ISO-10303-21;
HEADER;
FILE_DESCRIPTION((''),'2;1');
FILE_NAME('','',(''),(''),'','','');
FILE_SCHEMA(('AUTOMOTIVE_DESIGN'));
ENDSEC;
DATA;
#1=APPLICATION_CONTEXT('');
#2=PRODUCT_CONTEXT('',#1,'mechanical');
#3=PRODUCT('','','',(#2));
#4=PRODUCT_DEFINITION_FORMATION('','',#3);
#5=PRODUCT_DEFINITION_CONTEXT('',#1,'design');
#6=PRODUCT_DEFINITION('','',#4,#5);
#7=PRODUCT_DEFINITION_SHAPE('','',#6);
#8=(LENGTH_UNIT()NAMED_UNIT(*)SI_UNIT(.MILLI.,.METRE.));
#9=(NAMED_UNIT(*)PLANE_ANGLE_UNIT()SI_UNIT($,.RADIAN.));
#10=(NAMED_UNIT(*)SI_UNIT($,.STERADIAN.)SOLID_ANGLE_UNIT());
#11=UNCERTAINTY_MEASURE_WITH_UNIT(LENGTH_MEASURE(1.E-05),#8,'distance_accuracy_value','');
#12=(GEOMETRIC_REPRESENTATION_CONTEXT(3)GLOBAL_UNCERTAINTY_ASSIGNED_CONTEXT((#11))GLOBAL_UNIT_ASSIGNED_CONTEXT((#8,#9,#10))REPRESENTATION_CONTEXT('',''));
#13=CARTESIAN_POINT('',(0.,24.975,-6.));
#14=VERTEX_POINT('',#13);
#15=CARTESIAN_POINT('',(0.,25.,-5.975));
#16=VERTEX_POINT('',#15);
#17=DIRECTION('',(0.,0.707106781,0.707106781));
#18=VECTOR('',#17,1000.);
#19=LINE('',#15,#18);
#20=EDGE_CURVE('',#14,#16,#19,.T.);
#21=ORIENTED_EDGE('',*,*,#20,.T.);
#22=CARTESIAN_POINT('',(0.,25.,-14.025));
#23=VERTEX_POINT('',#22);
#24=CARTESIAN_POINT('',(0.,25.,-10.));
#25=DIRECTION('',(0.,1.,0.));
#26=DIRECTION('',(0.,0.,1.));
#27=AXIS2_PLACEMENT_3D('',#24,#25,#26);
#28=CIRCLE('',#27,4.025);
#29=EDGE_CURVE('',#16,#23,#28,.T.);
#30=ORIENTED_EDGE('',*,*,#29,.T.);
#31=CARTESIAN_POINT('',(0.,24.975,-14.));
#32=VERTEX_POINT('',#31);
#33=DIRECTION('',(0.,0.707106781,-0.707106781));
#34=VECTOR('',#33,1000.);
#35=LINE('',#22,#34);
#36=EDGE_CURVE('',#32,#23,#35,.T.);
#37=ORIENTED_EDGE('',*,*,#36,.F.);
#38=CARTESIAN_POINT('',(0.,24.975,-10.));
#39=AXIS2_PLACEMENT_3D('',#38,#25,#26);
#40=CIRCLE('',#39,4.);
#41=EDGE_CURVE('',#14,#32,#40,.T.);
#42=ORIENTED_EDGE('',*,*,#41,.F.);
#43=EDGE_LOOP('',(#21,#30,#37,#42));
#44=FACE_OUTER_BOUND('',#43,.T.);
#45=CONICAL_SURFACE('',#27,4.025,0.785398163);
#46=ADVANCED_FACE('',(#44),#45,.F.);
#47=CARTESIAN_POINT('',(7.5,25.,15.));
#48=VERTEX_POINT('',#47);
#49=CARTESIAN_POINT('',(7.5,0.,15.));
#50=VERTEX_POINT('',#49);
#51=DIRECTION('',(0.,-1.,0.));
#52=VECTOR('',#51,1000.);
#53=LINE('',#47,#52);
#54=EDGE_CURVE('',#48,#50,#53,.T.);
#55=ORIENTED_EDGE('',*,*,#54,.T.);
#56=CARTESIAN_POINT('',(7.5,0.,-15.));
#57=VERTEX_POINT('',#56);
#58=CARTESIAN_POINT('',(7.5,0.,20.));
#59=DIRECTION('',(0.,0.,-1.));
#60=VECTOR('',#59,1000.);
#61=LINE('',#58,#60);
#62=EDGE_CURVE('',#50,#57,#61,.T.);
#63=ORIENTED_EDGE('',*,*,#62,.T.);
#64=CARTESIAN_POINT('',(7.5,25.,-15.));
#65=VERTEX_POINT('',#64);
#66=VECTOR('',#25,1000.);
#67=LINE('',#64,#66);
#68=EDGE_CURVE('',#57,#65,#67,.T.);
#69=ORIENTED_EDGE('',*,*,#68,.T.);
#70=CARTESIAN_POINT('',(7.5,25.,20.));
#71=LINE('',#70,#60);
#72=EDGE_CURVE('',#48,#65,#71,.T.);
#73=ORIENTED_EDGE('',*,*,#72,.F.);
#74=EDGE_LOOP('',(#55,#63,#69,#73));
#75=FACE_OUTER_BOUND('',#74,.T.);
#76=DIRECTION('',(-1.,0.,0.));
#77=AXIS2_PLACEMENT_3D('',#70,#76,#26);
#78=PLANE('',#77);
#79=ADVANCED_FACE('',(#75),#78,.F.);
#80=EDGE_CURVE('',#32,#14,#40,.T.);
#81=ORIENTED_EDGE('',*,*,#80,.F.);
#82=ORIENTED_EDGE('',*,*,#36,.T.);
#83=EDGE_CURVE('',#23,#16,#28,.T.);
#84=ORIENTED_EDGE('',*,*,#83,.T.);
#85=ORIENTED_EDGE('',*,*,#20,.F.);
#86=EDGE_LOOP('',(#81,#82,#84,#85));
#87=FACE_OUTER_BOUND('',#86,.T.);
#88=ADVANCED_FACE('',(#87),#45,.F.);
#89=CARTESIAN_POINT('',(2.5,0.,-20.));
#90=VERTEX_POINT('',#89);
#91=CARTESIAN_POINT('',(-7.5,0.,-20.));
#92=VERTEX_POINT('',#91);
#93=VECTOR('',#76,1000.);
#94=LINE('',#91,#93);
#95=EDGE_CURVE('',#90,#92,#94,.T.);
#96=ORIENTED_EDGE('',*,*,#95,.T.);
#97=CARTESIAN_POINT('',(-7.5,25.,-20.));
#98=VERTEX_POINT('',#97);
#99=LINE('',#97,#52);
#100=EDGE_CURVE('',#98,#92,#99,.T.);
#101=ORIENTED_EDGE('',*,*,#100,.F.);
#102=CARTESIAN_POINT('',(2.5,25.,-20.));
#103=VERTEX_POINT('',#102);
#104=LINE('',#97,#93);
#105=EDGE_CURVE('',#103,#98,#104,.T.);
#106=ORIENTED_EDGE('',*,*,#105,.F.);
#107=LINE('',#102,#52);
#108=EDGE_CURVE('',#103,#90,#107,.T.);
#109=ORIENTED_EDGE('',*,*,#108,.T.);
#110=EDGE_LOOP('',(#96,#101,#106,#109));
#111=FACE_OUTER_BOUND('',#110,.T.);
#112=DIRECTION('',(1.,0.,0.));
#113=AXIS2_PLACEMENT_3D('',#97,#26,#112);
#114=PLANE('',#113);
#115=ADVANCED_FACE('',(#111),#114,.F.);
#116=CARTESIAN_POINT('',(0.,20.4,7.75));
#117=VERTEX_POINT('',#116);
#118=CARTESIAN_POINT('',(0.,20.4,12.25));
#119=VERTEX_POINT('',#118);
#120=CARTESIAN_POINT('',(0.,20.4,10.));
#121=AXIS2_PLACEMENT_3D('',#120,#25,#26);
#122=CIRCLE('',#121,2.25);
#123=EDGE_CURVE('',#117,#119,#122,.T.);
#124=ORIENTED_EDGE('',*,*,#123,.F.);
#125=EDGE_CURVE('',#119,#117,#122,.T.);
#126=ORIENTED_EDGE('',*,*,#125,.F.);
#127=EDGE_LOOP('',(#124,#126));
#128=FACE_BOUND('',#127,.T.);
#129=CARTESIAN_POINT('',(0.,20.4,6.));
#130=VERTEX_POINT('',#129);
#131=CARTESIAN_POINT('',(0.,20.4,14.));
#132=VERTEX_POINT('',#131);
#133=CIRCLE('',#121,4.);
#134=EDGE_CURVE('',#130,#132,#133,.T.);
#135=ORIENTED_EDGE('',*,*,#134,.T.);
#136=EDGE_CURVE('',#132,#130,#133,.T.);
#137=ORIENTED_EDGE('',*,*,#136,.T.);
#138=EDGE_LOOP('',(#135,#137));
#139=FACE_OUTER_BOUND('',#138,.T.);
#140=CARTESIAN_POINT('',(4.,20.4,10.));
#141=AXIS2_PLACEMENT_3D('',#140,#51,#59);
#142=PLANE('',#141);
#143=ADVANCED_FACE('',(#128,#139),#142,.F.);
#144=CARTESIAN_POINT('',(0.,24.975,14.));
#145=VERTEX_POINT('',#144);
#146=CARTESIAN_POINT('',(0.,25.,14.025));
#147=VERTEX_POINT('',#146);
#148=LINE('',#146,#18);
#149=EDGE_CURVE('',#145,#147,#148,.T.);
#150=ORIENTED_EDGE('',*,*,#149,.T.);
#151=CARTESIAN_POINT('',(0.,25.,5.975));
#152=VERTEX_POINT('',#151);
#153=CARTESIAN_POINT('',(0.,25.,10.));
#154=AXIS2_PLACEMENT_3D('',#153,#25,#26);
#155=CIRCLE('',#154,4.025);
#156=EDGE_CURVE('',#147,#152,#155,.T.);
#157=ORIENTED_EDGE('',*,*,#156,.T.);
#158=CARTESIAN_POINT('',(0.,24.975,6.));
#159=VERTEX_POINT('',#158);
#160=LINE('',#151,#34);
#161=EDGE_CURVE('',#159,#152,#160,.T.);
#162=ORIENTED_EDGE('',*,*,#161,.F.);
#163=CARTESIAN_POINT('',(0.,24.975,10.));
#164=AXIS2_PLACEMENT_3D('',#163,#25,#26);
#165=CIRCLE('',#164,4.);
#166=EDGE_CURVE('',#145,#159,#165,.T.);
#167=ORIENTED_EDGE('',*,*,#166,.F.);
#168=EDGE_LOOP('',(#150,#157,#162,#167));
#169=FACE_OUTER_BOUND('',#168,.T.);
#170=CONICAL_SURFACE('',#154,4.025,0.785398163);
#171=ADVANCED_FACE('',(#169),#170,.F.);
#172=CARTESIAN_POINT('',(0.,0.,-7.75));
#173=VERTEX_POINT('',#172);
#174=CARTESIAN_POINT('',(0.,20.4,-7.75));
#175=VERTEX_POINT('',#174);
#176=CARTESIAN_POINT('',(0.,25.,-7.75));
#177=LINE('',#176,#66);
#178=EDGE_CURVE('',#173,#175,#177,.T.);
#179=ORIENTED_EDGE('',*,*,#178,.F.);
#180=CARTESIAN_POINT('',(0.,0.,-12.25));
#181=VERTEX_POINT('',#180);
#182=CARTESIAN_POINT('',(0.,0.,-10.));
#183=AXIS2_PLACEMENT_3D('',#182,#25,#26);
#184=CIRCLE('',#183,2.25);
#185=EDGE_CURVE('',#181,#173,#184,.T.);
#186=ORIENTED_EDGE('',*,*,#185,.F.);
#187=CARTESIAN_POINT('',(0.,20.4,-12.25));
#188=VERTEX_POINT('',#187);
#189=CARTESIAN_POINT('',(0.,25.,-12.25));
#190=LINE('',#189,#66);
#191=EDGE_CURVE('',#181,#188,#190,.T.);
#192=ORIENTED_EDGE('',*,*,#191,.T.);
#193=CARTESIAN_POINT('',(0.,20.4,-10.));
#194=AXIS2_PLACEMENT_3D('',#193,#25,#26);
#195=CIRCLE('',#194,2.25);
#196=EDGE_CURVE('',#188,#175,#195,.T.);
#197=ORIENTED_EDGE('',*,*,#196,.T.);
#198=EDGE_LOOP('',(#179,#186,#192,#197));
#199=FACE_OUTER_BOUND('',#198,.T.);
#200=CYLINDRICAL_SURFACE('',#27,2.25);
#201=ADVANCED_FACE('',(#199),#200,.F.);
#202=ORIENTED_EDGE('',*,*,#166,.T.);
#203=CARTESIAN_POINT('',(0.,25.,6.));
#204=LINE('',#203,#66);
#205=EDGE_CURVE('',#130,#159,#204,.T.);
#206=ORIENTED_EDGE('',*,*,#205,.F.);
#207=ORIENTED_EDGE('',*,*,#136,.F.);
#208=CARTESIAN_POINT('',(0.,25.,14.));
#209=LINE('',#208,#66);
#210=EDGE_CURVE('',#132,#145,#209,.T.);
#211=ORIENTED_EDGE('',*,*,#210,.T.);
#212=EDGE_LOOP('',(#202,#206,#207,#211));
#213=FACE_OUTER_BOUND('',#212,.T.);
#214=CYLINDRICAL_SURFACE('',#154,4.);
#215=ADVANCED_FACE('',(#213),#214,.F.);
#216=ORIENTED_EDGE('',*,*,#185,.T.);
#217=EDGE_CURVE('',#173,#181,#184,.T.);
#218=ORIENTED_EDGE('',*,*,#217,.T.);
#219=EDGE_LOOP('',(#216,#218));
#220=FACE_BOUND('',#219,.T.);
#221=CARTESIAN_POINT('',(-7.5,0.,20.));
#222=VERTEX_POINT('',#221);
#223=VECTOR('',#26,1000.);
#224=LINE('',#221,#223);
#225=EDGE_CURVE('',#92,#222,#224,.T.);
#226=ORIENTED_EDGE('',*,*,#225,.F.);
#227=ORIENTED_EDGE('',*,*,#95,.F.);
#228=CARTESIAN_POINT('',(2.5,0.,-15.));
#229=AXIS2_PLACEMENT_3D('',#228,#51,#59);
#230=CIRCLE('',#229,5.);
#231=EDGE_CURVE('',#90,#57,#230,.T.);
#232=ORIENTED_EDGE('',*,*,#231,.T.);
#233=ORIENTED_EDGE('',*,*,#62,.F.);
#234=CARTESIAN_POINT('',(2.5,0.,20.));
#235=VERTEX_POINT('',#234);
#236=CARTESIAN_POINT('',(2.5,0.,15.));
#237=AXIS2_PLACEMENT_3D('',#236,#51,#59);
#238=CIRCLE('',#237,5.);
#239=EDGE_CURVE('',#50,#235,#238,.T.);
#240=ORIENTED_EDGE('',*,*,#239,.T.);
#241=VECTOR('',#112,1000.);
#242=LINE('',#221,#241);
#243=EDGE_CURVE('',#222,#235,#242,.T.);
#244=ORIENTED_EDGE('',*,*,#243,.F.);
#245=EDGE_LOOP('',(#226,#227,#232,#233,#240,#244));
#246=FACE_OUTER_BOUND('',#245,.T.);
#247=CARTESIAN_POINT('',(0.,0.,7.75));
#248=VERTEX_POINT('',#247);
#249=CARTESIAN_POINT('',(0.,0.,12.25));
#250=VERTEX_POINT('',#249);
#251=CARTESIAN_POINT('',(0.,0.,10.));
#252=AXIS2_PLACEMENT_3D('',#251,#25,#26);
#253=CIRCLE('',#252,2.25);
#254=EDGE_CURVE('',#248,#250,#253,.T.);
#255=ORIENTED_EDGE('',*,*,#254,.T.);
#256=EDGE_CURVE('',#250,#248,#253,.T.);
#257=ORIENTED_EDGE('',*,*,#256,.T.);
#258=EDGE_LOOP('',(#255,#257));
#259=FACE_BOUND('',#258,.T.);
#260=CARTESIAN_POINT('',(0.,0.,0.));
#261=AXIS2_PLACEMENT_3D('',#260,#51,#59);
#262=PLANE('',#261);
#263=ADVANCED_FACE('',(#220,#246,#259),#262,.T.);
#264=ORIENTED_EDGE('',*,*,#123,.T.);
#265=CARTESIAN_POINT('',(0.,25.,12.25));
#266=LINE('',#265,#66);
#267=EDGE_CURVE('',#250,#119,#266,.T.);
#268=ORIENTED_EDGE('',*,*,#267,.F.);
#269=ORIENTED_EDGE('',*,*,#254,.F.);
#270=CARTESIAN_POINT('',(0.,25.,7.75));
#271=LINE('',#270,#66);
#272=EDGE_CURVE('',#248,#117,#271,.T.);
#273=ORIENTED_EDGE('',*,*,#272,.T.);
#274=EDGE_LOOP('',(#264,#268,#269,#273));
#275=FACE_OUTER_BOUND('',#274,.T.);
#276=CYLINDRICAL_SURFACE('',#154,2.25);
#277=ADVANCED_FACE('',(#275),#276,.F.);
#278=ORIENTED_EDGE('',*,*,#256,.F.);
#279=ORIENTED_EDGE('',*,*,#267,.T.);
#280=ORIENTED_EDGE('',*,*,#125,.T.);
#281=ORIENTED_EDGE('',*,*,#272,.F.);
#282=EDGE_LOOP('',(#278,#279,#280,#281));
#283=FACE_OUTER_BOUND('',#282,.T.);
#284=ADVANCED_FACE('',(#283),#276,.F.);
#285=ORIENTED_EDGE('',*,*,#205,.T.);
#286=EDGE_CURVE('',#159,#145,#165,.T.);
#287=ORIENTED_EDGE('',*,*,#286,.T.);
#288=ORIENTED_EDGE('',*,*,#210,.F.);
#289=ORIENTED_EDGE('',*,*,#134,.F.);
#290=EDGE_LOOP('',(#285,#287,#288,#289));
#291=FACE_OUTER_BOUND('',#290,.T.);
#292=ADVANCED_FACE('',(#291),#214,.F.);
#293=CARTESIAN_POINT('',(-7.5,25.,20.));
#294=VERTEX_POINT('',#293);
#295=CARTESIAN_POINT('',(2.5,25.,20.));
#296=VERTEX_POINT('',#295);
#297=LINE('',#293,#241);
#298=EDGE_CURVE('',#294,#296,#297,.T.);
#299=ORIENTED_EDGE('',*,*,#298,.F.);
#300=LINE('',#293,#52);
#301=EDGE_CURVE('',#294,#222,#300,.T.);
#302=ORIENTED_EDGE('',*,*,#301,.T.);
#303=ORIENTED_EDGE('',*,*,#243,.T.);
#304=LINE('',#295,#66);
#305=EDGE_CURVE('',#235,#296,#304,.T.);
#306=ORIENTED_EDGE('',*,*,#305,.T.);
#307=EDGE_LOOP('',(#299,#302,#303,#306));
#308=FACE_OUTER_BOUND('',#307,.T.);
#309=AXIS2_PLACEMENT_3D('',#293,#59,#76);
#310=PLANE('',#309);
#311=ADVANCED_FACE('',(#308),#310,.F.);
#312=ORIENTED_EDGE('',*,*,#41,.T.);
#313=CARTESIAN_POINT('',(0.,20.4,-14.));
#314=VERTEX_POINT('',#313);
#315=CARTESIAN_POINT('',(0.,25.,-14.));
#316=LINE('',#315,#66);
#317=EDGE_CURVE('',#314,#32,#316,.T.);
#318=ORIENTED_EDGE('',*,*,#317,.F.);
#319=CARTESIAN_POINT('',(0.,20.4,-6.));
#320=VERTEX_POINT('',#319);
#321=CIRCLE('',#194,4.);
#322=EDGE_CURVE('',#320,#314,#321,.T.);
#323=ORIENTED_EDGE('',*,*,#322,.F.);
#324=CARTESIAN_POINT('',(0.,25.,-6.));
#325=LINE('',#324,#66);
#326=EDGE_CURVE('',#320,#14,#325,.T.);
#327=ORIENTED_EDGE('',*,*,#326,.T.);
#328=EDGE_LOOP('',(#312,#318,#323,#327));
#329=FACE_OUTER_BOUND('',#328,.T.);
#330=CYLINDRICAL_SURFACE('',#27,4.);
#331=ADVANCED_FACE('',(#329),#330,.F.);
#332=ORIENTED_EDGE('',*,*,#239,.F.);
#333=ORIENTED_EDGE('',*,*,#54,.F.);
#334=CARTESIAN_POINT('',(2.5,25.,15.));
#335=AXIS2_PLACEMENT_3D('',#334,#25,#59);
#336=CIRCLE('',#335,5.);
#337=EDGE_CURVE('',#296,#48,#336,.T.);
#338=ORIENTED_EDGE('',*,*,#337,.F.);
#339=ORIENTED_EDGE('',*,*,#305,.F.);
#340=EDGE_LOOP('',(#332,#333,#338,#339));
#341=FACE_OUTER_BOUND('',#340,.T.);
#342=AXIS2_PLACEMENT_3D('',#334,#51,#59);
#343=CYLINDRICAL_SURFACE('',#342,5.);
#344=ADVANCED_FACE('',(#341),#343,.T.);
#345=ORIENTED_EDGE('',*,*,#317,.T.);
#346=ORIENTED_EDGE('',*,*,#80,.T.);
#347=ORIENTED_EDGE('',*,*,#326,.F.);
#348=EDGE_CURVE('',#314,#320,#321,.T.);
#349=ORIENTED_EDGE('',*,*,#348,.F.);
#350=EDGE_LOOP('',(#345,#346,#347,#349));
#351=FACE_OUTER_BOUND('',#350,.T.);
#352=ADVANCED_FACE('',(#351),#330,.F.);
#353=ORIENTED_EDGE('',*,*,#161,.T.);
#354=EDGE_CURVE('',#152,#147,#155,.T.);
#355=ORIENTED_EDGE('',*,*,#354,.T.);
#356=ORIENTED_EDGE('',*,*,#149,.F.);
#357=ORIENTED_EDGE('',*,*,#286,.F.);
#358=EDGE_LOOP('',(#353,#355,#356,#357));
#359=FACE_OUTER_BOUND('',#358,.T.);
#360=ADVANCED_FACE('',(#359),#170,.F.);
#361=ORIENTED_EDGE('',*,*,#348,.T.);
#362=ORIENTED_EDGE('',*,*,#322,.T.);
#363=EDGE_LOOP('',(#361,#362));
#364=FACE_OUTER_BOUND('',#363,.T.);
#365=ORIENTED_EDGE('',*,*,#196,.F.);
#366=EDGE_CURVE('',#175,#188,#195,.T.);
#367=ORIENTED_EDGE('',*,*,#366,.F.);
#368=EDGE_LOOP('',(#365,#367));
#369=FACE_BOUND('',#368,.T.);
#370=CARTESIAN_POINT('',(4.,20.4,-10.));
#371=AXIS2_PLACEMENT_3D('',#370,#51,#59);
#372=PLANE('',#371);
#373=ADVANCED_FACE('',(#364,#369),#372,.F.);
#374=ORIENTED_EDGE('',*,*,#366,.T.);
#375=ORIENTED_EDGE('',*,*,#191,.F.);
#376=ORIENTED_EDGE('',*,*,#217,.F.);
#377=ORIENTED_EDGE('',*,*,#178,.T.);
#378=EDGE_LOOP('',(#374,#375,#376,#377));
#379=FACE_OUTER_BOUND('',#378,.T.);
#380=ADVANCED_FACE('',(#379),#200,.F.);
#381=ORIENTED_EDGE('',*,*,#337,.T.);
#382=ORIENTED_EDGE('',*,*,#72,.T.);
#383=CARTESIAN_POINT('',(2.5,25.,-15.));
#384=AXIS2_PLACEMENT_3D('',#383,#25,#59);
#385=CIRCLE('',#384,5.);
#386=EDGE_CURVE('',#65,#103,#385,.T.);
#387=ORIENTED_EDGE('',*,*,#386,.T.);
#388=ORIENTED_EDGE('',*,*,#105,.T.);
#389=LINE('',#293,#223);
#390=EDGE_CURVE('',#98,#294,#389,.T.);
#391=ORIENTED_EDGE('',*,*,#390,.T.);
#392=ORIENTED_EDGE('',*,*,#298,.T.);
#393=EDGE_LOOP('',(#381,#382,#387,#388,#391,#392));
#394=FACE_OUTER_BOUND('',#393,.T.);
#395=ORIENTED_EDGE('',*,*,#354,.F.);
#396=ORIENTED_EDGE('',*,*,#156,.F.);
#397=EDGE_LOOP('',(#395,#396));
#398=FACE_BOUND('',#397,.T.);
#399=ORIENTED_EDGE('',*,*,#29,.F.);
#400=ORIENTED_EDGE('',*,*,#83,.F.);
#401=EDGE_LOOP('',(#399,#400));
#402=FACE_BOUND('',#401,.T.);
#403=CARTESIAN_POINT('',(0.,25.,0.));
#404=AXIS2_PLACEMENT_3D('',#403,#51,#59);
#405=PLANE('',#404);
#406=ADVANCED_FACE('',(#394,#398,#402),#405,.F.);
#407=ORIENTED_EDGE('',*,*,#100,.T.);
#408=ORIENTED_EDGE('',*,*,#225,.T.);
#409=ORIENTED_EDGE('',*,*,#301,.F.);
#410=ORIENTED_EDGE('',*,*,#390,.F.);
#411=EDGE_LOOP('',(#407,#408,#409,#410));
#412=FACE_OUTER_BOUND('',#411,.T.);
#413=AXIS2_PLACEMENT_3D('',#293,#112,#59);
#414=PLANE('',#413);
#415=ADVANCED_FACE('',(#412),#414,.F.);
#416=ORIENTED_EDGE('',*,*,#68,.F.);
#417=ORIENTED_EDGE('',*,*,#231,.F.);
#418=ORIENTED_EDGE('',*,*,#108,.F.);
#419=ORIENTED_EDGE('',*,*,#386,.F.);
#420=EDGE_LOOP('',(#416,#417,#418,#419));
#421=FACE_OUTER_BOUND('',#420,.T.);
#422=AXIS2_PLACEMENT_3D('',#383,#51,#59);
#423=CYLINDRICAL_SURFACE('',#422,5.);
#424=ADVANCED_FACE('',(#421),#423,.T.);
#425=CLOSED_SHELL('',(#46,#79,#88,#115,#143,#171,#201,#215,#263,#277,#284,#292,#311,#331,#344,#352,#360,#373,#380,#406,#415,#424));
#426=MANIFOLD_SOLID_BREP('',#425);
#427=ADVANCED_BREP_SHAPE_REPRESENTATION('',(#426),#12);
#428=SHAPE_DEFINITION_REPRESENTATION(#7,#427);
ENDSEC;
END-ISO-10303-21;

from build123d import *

# Parameters (mm, degrees)
SKETCH1_W                                 = 15
SKETCH1_H                                 = 40
BOSS_EXTRUDE1_DEPTH                       = 25
FILLET1_R                                 = 5
HOLE_WIZARD_SOCKET_HEAD_CAP_SCREW_2_COUNT = 2
HOLE_WIZARD_SOCKET_HEAD_CAP_SCREW_2_PITCH = 20


with BuildPart() as part:
    # Sketch1 → Boss-Extrude1 (new body)
    with BuildSketch(Plane(origin=(0, 0, 0), x_dir=(1, 0, 0), z_dir=(0, 1, 0))):
        Rectangle(SKETCH1_W, SKETCH1_H)
    extrude(amount=BOSS_EXTRUDE1_DEPTH)

    # Fillet1
    fillet1_edges = [part.edges().sort_by_distance(p)[0] for p in [
        (7.5, 12.5, 20),
        (7.5, 12.5, -20),
    ]]
    fillet(fillet1_edges, radius=FILLET1_R)

    # Sketch3 → Hole wizard: socket head cap screw, type 1 (revolve, cut)
    with BuildSketch(Plane(origin=(0, 25, -10), x_dir=(0, 0, 1), z_dir=(1, 0, 0))):
        Polygon((0, 0), (0, 25), (2.25, 25), (2.25, 4.6), (4, 4.6), (4, 0.025), (4.025, 0), align=None)
    hole_wizard_socket_head_cap_screw_type = revolve(axis=Axis((0, 31.35, -10), (0, -1, 0)), mode=Mode.SUBTRACT)

    # Hole wizard_ socket head cap screw_  2: Hole wizard: socket head cap screw, type 1 ×2
    with Locations(*[(0, 0, i * HOLE_WIZARD_SOCKET_HEAD_CAP_SCREW_2_PITCH) for i in range(1, HOLE_WIZARD_SOCKET_HEAD_CAP_SCREW_2_COUNT)]):
        add(hole_wizard_socket_head_cap_screw_type, mode=Mode.SUBTRACT)


solid = part.part
